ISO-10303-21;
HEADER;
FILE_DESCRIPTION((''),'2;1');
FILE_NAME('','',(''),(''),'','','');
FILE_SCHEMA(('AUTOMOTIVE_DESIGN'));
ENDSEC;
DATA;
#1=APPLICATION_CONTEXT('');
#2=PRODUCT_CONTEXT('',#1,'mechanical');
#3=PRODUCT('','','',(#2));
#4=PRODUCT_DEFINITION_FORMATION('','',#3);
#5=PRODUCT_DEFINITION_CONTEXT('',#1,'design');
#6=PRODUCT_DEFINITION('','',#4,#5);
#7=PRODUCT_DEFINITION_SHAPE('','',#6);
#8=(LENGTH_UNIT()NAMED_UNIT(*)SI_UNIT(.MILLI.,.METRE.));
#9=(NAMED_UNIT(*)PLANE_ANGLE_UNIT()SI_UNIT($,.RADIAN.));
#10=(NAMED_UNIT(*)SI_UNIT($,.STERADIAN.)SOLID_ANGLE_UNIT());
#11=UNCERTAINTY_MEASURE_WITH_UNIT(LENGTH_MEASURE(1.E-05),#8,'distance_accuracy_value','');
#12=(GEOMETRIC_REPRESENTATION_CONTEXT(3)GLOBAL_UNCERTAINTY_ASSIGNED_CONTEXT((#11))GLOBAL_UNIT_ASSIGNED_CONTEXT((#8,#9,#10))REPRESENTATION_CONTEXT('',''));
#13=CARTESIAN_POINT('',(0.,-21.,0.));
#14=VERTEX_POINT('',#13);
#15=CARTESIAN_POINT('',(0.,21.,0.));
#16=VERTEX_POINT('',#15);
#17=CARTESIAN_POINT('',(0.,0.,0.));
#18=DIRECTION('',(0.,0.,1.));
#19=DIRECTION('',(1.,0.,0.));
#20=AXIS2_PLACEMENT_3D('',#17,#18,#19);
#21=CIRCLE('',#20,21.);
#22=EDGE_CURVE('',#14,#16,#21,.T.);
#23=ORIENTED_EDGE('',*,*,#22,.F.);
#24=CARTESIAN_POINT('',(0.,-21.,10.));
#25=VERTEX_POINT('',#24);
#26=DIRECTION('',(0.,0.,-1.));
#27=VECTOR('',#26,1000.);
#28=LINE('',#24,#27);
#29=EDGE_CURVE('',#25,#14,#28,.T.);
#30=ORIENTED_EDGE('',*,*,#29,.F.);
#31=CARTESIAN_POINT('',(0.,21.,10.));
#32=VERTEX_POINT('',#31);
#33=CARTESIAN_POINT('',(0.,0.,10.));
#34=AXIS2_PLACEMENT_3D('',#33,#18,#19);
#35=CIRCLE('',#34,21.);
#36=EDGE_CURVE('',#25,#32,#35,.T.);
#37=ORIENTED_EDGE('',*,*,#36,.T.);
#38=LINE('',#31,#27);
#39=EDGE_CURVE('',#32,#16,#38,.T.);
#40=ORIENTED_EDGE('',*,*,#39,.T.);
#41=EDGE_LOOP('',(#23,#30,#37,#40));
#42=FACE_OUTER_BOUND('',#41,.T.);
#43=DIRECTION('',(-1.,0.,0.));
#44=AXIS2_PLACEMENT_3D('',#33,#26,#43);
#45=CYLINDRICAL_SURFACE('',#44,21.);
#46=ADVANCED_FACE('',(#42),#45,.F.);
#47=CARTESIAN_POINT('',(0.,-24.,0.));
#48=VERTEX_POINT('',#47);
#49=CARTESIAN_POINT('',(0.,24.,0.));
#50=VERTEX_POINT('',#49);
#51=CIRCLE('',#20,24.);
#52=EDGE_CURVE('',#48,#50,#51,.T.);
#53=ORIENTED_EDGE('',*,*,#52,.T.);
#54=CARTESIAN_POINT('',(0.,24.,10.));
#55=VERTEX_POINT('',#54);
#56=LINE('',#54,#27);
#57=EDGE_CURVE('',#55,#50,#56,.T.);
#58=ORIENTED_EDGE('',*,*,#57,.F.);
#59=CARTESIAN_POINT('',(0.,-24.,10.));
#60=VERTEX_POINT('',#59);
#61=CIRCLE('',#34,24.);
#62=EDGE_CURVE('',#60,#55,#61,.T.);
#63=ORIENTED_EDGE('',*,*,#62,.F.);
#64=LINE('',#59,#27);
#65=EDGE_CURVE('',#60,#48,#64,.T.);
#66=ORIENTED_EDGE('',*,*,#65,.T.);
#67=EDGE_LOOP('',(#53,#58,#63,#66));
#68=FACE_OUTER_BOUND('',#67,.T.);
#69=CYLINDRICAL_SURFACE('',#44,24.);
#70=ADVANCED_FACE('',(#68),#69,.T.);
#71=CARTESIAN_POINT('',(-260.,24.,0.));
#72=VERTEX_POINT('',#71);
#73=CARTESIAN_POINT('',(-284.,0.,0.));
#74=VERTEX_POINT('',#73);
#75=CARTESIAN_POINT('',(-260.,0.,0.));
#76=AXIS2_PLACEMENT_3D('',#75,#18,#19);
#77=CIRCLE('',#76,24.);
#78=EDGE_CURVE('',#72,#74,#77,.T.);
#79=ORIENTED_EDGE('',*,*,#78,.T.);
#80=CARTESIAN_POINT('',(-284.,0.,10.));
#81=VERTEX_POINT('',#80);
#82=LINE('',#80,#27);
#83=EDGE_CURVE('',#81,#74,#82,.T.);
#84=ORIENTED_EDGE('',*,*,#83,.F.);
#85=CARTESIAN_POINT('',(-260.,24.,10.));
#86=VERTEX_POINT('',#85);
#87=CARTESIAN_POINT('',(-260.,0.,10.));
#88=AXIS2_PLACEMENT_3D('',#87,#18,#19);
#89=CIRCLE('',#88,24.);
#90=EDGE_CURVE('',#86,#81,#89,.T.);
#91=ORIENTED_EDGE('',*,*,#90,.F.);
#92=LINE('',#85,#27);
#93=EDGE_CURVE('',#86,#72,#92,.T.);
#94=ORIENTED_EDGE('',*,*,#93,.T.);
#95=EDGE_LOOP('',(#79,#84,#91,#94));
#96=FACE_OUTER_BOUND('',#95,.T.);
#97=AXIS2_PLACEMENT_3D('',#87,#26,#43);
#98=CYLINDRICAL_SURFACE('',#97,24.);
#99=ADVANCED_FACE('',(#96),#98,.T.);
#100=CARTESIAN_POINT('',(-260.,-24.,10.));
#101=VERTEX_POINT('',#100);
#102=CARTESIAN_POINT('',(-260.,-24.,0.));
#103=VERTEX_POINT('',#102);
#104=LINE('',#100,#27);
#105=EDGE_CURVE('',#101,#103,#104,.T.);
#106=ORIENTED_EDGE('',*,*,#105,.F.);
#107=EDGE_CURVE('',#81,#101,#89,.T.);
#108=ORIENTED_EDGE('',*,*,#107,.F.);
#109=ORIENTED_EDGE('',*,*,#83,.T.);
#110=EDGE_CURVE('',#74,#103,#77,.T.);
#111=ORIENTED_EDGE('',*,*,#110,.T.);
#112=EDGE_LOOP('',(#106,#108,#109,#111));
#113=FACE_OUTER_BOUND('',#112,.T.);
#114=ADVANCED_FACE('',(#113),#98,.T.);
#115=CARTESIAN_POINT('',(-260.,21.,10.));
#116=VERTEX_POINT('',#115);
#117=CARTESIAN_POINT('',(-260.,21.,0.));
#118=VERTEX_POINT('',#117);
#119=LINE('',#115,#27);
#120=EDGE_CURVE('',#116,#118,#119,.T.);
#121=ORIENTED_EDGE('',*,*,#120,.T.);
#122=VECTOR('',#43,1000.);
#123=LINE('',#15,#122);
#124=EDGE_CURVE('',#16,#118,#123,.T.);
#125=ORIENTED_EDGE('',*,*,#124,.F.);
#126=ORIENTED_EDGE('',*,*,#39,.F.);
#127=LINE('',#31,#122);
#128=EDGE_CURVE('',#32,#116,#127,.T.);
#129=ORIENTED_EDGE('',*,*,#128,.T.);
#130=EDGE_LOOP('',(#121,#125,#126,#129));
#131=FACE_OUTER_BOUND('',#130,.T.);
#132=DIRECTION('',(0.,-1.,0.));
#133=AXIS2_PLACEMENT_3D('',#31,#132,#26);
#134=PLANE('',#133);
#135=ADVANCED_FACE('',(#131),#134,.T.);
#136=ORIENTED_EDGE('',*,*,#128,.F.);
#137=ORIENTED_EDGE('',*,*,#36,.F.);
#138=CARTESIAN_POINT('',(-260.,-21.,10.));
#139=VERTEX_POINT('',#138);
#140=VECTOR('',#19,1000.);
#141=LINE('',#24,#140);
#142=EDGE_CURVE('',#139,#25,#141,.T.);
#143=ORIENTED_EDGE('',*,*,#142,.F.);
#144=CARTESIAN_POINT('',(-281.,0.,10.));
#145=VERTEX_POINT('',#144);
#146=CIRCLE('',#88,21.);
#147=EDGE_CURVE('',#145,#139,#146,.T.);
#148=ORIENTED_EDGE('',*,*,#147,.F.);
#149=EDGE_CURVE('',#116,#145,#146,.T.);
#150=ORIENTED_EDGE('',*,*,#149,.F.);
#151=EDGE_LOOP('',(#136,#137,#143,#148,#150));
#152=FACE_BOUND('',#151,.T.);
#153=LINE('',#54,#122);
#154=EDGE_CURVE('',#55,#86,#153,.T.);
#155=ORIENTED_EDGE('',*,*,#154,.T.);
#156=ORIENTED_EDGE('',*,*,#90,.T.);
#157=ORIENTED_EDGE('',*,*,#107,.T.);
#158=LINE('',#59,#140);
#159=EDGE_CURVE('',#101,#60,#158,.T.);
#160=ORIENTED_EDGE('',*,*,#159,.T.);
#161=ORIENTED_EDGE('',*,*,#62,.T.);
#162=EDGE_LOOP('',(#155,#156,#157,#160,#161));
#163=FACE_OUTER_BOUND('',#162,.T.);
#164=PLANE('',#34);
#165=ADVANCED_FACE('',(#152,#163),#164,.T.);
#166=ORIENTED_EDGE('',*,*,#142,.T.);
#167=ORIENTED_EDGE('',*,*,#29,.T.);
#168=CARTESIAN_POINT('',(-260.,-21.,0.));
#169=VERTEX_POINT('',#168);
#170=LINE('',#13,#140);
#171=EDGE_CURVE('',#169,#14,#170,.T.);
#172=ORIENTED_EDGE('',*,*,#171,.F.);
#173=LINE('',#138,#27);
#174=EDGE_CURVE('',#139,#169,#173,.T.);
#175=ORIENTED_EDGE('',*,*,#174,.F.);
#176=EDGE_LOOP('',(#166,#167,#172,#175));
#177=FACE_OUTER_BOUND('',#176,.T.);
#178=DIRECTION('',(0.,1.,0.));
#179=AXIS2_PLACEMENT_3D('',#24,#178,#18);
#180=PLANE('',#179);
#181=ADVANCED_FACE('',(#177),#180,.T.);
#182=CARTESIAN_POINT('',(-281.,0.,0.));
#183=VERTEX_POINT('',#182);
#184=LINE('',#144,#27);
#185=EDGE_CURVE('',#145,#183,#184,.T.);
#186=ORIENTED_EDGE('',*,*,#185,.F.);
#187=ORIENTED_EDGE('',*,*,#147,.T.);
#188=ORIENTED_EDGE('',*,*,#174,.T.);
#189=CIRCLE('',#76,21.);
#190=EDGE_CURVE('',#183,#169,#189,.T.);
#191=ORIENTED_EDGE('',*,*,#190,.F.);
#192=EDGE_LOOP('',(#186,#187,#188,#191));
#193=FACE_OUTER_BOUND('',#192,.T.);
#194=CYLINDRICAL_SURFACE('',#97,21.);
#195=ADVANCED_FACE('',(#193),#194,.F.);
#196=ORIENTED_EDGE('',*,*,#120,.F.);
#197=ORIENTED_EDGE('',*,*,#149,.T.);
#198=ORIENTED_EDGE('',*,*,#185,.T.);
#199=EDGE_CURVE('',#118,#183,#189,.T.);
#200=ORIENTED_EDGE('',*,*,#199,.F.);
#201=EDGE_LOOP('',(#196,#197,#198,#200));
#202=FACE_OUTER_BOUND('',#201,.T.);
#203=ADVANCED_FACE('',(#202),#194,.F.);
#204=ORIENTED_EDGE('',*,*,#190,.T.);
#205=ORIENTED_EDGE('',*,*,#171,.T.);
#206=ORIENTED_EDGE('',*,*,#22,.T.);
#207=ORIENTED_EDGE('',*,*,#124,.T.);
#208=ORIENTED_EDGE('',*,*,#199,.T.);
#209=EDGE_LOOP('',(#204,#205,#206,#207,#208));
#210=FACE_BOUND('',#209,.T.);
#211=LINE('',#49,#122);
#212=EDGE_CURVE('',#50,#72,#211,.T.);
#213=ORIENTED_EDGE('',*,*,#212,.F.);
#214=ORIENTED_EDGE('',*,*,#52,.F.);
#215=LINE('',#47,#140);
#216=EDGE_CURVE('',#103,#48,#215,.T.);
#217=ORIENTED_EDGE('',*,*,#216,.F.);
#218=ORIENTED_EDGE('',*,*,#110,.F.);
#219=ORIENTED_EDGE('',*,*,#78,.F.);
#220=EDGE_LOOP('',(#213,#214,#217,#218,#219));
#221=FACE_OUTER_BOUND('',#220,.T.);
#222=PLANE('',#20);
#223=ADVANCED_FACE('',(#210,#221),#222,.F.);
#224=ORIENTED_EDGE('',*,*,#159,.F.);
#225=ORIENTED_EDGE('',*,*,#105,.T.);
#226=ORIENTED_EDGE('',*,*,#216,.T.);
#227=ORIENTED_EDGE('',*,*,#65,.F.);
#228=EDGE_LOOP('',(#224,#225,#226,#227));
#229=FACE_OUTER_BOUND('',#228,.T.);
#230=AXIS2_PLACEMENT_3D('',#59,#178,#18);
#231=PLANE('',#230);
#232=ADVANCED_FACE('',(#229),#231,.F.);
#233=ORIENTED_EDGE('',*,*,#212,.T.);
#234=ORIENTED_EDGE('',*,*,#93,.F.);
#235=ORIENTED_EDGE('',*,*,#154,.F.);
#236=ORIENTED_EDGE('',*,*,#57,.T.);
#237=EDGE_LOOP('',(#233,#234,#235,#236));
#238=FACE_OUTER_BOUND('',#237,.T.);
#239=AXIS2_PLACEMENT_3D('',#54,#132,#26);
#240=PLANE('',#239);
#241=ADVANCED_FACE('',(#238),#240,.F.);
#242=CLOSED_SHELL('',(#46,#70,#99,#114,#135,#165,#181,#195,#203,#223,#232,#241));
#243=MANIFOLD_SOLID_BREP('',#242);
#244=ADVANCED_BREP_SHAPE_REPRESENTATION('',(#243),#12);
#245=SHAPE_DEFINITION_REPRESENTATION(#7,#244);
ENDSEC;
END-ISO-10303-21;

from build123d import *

# Parameters (mm, degrees)
BOSS_EXTRUDE1_DEPTH = 10
SHELL1_T            = -3


with BuildPart() as part:
    # Sketch2 → Boss-Extrude1 (new body)
    with BuildSketch(Plane.XY):
        with BuildLine():
            Line((0, 24), (-260, 24))
            ThreePointArc((-260, 24), (-284, 0), (-260, -24))
            Line((-260, -24), (0, -24))
            ThreePointArc((0, -24), (24, 0), (0, 24))
        make_face()
    extrude(amount=BOSS_EXTRUDE1_DEPTH)

    # Shell1
    shell1_openings = [part.faces().sort_by_distance(p)[0] for p in [
        (-130, 0, 10),
        (-130, 0, 0),
    ]]
    offset(amount=SHELL1_T, openings=shell1_openings, kind=Kind.INTERSECTION)


solid = part.part
